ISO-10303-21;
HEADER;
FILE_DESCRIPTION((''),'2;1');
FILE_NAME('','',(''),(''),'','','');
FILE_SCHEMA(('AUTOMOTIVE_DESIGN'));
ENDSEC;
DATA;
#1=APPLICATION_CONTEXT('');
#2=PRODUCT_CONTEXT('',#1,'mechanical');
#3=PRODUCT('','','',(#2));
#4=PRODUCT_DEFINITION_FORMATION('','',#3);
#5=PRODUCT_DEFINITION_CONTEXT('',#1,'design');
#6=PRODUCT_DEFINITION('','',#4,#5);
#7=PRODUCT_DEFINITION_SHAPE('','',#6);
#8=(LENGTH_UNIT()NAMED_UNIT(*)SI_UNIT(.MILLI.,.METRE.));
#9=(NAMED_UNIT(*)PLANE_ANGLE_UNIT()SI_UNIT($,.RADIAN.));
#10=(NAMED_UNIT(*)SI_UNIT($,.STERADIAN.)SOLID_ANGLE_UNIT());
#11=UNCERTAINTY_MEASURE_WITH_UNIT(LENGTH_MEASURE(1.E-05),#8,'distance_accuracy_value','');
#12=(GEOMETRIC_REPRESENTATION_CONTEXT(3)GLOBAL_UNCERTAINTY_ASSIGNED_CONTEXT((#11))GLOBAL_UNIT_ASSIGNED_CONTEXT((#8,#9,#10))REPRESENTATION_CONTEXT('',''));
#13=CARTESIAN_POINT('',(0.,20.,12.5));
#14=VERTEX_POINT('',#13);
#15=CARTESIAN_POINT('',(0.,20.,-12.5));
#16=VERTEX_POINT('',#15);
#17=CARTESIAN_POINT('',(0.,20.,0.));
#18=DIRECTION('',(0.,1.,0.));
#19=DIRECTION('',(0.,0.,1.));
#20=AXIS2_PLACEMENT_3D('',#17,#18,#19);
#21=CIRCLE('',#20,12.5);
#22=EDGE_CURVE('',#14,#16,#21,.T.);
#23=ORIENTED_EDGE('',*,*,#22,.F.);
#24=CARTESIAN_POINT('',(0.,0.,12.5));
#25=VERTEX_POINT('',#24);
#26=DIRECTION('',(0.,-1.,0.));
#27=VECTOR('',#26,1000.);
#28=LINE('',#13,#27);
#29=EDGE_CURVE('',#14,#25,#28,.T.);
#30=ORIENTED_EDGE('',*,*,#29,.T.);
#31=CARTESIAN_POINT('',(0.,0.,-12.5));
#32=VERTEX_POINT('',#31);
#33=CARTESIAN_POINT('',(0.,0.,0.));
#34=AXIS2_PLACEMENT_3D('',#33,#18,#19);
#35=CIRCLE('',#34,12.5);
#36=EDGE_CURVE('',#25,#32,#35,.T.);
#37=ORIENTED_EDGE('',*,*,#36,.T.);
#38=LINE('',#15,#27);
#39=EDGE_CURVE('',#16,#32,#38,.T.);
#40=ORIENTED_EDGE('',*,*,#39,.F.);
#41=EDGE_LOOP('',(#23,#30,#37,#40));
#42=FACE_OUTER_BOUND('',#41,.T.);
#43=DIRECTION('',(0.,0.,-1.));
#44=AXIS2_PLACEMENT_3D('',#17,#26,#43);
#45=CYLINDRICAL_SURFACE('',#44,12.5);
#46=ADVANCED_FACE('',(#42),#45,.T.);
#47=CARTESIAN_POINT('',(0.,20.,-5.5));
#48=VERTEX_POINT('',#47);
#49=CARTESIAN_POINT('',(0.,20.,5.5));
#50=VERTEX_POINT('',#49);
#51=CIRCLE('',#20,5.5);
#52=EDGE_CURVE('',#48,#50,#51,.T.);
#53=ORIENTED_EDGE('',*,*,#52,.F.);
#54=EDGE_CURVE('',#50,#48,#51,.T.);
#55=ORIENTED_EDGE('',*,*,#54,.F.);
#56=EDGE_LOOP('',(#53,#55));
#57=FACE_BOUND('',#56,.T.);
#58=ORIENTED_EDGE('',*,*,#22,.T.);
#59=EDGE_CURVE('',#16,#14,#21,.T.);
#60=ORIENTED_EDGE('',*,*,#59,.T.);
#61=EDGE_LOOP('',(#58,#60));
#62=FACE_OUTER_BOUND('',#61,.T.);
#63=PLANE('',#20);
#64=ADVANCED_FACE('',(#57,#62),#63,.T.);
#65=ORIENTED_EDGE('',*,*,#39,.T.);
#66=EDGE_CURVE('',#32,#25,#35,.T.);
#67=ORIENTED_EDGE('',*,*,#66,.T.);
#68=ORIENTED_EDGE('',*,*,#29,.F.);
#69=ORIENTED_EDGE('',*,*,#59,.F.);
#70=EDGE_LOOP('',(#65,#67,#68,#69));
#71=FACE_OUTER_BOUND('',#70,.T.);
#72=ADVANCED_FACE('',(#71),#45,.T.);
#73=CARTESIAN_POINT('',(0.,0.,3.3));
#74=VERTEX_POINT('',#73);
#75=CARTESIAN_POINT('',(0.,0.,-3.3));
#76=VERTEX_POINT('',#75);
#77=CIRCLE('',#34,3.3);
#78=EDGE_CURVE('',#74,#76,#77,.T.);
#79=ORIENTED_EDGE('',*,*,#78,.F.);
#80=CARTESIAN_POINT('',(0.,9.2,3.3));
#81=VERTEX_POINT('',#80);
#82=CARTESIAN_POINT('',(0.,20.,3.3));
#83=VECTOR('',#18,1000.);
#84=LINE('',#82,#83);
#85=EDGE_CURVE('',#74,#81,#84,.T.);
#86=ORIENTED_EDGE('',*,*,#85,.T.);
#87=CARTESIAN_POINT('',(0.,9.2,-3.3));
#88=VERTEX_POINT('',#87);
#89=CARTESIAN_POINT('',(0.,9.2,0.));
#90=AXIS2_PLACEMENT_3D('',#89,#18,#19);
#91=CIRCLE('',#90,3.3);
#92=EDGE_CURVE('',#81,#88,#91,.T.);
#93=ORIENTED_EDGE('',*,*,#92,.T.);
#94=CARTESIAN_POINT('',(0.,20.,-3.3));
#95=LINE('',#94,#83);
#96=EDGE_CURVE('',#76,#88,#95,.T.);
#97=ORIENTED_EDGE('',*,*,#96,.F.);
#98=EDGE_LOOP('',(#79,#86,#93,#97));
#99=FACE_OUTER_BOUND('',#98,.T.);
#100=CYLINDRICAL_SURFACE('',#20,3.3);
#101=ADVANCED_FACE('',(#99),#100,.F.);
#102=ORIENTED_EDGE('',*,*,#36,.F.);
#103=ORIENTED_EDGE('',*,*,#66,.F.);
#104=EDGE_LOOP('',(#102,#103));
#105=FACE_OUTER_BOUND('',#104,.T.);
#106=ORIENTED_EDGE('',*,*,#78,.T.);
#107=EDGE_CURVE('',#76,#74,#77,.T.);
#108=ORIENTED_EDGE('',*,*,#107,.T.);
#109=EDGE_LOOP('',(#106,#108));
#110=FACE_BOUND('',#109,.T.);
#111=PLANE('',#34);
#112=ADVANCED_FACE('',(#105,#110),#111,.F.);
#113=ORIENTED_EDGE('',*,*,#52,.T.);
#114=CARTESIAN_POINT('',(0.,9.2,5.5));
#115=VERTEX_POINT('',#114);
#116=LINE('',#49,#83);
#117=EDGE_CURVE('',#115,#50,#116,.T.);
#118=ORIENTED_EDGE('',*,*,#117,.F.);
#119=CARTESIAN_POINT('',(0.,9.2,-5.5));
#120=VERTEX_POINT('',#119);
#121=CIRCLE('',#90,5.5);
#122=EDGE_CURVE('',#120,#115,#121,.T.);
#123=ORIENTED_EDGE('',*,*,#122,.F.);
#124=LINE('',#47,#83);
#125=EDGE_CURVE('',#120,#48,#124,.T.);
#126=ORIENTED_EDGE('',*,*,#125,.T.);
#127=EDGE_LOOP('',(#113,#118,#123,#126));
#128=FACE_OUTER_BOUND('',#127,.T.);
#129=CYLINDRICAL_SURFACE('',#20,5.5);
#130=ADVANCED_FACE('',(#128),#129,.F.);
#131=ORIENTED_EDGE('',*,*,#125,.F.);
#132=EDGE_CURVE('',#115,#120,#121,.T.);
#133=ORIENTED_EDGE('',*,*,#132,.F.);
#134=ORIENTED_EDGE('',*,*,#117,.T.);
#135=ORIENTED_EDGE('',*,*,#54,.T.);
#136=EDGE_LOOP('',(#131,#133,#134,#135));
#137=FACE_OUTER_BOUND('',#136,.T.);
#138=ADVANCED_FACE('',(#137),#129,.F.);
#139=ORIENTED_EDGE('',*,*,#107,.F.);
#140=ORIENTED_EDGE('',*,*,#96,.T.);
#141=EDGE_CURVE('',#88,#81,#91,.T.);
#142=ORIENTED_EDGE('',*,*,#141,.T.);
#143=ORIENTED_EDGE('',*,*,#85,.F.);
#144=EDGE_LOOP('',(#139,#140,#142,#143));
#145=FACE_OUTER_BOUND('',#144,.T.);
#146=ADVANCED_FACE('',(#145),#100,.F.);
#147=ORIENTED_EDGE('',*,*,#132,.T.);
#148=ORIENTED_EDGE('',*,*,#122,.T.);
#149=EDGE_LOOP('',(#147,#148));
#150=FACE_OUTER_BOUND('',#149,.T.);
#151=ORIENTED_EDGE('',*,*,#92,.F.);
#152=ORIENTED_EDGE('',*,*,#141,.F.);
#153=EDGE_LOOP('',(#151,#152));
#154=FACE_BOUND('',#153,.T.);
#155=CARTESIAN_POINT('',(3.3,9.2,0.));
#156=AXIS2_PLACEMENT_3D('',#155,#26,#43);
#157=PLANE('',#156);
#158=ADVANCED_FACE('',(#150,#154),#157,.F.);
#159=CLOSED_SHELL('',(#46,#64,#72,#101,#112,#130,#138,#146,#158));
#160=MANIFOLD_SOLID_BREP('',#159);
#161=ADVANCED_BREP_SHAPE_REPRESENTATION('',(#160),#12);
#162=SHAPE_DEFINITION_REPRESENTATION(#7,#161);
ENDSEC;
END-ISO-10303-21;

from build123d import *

# Parameters (mm, degrees)
SKETCH_1_R                   = 12.5
EXTRUDE_1_DEPTH              = 20
HOLE_WIZARD_M6_1_D           = 6.6
HOLE_WIZARD_M6_1_CBORE_D     = 11
HOLE_WIZARD_M6_1_CBORE_DEPTH = 10.8


with BuildPart() as part:
    # 草图1 → 凸台-拉伸1 (new body)
    with BuildSketch(Plane(origin=(0, 0, 0), x_dir=(1, 0, 0), z_dir=(0, 1, 0))):
        with Locations(Location((0, 0, 0), (0, 0, 270))):
            Circle(SKETCH_1_R)
    extrude(amount=EXTRUDE_1_DEPTH)

    # M6 六角圆柱头螺钉的柱形沉头孔1 (through all)
    with Locations(Plane(origin=(0, 20, 0), x_dir=(1, 0, 0), z_dir=(0, 1, 0))):
        with Locations((0, 0)):
            CounterBoreHole(HOLE_WIZARD_M6_1_D / 2, HOLE_WIZARD_M6_1_CBORE_D / 2, HOLE_WIZARD_M6_1_CBORE_DEPTH)


solid = part.part
